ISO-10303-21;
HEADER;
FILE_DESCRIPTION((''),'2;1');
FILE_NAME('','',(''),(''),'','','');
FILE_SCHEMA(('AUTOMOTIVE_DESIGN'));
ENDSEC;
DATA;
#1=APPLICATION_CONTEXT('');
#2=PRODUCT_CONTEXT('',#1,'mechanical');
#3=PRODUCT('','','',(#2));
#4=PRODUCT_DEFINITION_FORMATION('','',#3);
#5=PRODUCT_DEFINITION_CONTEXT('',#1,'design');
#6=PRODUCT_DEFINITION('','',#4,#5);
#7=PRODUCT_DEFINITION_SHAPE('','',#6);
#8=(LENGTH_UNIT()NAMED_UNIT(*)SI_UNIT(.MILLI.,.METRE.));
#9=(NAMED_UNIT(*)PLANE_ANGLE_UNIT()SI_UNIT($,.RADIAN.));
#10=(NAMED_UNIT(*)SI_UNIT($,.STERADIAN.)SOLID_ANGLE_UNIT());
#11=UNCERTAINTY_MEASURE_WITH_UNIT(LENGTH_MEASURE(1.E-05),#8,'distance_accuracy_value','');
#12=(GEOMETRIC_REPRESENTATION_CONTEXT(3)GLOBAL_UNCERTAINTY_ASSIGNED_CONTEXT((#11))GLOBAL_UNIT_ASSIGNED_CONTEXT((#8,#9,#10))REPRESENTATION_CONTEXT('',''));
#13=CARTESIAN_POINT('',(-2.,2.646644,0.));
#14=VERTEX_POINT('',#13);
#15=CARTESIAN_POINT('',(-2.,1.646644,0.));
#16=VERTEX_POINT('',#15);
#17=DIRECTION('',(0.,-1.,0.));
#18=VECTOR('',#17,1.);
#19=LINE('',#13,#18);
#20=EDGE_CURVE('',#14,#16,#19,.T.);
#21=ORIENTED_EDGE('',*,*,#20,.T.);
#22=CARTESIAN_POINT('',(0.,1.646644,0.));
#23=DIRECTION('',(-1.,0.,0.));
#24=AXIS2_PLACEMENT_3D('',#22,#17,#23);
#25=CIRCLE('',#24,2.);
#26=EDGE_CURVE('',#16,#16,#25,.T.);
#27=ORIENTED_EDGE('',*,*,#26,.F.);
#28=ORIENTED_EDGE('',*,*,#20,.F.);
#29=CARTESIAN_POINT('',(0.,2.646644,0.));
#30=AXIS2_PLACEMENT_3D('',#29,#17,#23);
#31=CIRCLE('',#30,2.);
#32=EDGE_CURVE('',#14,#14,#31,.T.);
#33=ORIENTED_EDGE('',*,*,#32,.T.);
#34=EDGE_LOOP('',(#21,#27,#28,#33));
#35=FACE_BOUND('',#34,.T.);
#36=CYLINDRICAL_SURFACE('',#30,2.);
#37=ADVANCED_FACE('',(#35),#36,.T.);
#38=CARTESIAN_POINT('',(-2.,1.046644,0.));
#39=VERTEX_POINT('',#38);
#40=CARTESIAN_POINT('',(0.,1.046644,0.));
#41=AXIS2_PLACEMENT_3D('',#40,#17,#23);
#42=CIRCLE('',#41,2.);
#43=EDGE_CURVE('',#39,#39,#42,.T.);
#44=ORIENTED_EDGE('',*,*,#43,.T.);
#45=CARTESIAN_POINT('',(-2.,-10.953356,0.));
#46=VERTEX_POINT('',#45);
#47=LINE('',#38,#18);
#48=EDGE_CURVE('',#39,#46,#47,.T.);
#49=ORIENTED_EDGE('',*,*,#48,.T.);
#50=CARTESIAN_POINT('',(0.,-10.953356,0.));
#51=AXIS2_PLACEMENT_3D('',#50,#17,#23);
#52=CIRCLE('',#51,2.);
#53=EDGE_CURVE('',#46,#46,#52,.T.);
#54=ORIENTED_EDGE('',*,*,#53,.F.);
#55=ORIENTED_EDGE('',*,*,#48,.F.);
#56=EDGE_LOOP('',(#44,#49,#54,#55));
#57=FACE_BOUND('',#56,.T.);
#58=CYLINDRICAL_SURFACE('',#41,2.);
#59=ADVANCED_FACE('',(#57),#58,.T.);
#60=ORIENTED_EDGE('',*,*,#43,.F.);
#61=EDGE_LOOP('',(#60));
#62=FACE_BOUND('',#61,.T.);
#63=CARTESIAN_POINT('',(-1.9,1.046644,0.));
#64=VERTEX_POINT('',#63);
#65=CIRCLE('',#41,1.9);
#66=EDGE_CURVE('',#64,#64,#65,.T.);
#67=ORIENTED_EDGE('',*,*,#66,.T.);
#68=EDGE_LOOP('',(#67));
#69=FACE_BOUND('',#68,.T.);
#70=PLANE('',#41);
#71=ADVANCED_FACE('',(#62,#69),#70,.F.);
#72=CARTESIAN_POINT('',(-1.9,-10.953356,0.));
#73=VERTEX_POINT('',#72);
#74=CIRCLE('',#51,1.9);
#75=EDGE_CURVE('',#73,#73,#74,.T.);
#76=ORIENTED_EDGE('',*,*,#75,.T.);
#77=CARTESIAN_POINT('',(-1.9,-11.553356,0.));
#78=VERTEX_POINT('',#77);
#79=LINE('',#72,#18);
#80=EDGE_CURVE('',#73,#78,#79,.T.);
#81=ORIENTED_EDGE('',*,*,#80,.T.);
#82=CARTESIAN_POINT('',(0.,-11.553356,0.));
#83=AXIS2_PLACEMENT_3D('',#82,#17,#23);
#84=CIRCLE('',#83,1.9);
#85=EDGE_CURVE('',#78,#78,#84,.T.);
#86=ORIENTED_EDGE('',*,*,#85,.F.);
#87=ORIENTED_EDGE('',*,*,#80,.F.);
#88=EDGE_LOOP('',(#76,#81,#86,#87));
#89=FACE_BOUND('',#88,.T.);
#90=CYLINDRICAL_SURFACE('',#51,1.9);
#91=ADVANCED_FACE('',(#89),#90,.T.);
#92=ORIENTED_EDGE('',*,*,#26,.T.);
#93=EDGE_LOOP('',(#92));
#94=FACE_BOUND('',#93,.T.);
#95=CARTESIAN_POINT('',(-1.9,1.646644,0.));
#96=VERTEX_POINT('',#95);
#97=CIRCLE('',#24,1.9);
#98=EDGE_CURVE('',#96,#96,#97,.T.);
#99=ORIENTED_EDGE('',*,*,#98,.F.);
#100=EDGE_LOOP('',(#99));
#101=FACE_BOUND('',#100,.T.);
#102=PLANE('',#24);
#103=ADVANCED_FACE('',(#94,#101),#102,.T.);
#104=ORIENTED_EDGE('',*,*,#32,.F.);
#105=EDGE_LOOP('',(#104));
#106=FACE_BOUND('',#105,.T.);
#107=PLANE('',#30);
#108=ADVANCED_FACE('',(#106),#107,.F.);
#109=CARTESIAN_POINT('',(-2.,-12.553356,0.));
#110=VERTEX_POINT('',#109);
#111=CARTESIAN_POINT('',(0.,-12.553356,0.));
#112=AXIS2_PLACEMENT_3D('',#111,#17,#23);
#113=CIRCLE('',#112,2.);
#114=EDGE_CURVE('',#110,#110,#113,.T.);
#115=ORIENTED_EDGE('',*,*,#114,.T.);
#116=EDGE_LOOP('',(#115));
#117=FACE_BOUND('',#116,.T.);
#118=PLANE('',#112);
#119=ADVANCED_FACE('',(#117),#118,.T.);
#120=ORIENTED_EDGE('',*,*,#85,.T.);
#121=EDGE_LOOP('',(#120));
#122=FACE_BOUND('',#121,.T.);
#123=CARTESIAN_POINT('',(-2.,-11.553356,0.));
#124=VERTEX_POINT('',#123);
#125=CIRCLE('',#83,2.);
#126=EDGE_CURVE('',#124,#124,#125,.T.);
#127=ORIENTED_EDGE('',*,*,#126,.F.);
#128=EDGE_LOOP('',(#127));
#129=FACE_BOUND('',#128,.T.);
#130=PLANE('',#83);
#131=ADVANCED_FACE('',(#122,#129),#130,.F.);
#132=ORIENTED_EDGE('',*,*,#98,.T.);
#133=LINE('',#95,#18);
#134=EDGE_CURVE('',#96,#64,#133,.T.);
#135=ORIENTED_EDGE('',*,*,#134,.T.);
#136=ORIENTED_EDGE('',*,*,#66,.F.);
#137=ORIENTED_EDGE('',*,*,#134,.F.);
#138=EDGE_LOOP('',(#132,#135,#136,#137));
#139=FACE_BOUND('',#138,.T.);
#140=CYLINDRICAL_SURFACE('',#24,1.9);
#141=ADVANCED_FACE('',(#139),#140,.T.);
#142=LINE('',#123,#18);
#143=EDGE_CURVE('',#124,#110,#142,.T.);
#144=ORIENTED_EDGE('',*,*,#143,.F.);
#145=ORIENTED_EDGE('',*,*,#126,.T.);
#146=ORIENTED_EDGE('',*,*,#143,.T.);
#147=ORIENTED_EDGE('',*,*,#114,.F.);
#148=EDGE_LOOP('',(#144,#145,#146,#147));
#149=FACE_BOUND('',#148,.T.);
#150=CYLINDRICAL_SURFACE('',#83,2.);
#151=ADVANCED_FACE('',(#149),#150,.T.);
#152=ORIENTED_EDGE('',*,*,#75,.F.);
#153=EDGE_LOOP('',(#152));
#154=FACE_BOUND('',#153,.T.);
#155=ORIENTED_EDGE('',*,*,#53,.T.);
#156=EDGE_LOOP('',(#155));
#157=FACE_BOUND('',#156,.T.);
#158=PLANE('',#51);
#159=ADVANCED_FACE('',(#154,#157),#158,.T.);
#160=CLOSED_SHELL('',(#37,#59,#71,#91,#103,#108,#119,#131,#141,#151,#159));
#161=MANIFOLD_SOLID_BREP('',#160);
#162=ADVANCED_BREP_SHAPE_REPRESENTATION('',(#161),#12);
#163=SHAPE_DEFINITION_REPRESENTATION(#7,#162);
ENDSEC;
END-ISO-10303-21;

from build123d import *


with BuildPart() as part:
    # 草图1 → 旋转1 (revolve)
    with BuildSketch(Plane.XY, mode=Mode.PRIVATE) as revolve_1_sk:
        Polygon((0, 2.646643634), (2, 2.646643634), (2, 1.646643634), (1.9, 1.646643634), (1.9, 1.046643634), (2, 1.046643634), (2, -10.953356366), (1.9, -10.953356366), (1.9, -11.553356366), (2, -11.553356366), (2, -12.553356366), (0, -12.553356366), align=None)
    revolve(revolve_1_sk.sketch.rotate(Axis((0, 2.646643634, 0), (0, -1, 0)), 180), axis=Axis((0, 2.646643634, 0), (0, -1, 0)))


solid = part.part
